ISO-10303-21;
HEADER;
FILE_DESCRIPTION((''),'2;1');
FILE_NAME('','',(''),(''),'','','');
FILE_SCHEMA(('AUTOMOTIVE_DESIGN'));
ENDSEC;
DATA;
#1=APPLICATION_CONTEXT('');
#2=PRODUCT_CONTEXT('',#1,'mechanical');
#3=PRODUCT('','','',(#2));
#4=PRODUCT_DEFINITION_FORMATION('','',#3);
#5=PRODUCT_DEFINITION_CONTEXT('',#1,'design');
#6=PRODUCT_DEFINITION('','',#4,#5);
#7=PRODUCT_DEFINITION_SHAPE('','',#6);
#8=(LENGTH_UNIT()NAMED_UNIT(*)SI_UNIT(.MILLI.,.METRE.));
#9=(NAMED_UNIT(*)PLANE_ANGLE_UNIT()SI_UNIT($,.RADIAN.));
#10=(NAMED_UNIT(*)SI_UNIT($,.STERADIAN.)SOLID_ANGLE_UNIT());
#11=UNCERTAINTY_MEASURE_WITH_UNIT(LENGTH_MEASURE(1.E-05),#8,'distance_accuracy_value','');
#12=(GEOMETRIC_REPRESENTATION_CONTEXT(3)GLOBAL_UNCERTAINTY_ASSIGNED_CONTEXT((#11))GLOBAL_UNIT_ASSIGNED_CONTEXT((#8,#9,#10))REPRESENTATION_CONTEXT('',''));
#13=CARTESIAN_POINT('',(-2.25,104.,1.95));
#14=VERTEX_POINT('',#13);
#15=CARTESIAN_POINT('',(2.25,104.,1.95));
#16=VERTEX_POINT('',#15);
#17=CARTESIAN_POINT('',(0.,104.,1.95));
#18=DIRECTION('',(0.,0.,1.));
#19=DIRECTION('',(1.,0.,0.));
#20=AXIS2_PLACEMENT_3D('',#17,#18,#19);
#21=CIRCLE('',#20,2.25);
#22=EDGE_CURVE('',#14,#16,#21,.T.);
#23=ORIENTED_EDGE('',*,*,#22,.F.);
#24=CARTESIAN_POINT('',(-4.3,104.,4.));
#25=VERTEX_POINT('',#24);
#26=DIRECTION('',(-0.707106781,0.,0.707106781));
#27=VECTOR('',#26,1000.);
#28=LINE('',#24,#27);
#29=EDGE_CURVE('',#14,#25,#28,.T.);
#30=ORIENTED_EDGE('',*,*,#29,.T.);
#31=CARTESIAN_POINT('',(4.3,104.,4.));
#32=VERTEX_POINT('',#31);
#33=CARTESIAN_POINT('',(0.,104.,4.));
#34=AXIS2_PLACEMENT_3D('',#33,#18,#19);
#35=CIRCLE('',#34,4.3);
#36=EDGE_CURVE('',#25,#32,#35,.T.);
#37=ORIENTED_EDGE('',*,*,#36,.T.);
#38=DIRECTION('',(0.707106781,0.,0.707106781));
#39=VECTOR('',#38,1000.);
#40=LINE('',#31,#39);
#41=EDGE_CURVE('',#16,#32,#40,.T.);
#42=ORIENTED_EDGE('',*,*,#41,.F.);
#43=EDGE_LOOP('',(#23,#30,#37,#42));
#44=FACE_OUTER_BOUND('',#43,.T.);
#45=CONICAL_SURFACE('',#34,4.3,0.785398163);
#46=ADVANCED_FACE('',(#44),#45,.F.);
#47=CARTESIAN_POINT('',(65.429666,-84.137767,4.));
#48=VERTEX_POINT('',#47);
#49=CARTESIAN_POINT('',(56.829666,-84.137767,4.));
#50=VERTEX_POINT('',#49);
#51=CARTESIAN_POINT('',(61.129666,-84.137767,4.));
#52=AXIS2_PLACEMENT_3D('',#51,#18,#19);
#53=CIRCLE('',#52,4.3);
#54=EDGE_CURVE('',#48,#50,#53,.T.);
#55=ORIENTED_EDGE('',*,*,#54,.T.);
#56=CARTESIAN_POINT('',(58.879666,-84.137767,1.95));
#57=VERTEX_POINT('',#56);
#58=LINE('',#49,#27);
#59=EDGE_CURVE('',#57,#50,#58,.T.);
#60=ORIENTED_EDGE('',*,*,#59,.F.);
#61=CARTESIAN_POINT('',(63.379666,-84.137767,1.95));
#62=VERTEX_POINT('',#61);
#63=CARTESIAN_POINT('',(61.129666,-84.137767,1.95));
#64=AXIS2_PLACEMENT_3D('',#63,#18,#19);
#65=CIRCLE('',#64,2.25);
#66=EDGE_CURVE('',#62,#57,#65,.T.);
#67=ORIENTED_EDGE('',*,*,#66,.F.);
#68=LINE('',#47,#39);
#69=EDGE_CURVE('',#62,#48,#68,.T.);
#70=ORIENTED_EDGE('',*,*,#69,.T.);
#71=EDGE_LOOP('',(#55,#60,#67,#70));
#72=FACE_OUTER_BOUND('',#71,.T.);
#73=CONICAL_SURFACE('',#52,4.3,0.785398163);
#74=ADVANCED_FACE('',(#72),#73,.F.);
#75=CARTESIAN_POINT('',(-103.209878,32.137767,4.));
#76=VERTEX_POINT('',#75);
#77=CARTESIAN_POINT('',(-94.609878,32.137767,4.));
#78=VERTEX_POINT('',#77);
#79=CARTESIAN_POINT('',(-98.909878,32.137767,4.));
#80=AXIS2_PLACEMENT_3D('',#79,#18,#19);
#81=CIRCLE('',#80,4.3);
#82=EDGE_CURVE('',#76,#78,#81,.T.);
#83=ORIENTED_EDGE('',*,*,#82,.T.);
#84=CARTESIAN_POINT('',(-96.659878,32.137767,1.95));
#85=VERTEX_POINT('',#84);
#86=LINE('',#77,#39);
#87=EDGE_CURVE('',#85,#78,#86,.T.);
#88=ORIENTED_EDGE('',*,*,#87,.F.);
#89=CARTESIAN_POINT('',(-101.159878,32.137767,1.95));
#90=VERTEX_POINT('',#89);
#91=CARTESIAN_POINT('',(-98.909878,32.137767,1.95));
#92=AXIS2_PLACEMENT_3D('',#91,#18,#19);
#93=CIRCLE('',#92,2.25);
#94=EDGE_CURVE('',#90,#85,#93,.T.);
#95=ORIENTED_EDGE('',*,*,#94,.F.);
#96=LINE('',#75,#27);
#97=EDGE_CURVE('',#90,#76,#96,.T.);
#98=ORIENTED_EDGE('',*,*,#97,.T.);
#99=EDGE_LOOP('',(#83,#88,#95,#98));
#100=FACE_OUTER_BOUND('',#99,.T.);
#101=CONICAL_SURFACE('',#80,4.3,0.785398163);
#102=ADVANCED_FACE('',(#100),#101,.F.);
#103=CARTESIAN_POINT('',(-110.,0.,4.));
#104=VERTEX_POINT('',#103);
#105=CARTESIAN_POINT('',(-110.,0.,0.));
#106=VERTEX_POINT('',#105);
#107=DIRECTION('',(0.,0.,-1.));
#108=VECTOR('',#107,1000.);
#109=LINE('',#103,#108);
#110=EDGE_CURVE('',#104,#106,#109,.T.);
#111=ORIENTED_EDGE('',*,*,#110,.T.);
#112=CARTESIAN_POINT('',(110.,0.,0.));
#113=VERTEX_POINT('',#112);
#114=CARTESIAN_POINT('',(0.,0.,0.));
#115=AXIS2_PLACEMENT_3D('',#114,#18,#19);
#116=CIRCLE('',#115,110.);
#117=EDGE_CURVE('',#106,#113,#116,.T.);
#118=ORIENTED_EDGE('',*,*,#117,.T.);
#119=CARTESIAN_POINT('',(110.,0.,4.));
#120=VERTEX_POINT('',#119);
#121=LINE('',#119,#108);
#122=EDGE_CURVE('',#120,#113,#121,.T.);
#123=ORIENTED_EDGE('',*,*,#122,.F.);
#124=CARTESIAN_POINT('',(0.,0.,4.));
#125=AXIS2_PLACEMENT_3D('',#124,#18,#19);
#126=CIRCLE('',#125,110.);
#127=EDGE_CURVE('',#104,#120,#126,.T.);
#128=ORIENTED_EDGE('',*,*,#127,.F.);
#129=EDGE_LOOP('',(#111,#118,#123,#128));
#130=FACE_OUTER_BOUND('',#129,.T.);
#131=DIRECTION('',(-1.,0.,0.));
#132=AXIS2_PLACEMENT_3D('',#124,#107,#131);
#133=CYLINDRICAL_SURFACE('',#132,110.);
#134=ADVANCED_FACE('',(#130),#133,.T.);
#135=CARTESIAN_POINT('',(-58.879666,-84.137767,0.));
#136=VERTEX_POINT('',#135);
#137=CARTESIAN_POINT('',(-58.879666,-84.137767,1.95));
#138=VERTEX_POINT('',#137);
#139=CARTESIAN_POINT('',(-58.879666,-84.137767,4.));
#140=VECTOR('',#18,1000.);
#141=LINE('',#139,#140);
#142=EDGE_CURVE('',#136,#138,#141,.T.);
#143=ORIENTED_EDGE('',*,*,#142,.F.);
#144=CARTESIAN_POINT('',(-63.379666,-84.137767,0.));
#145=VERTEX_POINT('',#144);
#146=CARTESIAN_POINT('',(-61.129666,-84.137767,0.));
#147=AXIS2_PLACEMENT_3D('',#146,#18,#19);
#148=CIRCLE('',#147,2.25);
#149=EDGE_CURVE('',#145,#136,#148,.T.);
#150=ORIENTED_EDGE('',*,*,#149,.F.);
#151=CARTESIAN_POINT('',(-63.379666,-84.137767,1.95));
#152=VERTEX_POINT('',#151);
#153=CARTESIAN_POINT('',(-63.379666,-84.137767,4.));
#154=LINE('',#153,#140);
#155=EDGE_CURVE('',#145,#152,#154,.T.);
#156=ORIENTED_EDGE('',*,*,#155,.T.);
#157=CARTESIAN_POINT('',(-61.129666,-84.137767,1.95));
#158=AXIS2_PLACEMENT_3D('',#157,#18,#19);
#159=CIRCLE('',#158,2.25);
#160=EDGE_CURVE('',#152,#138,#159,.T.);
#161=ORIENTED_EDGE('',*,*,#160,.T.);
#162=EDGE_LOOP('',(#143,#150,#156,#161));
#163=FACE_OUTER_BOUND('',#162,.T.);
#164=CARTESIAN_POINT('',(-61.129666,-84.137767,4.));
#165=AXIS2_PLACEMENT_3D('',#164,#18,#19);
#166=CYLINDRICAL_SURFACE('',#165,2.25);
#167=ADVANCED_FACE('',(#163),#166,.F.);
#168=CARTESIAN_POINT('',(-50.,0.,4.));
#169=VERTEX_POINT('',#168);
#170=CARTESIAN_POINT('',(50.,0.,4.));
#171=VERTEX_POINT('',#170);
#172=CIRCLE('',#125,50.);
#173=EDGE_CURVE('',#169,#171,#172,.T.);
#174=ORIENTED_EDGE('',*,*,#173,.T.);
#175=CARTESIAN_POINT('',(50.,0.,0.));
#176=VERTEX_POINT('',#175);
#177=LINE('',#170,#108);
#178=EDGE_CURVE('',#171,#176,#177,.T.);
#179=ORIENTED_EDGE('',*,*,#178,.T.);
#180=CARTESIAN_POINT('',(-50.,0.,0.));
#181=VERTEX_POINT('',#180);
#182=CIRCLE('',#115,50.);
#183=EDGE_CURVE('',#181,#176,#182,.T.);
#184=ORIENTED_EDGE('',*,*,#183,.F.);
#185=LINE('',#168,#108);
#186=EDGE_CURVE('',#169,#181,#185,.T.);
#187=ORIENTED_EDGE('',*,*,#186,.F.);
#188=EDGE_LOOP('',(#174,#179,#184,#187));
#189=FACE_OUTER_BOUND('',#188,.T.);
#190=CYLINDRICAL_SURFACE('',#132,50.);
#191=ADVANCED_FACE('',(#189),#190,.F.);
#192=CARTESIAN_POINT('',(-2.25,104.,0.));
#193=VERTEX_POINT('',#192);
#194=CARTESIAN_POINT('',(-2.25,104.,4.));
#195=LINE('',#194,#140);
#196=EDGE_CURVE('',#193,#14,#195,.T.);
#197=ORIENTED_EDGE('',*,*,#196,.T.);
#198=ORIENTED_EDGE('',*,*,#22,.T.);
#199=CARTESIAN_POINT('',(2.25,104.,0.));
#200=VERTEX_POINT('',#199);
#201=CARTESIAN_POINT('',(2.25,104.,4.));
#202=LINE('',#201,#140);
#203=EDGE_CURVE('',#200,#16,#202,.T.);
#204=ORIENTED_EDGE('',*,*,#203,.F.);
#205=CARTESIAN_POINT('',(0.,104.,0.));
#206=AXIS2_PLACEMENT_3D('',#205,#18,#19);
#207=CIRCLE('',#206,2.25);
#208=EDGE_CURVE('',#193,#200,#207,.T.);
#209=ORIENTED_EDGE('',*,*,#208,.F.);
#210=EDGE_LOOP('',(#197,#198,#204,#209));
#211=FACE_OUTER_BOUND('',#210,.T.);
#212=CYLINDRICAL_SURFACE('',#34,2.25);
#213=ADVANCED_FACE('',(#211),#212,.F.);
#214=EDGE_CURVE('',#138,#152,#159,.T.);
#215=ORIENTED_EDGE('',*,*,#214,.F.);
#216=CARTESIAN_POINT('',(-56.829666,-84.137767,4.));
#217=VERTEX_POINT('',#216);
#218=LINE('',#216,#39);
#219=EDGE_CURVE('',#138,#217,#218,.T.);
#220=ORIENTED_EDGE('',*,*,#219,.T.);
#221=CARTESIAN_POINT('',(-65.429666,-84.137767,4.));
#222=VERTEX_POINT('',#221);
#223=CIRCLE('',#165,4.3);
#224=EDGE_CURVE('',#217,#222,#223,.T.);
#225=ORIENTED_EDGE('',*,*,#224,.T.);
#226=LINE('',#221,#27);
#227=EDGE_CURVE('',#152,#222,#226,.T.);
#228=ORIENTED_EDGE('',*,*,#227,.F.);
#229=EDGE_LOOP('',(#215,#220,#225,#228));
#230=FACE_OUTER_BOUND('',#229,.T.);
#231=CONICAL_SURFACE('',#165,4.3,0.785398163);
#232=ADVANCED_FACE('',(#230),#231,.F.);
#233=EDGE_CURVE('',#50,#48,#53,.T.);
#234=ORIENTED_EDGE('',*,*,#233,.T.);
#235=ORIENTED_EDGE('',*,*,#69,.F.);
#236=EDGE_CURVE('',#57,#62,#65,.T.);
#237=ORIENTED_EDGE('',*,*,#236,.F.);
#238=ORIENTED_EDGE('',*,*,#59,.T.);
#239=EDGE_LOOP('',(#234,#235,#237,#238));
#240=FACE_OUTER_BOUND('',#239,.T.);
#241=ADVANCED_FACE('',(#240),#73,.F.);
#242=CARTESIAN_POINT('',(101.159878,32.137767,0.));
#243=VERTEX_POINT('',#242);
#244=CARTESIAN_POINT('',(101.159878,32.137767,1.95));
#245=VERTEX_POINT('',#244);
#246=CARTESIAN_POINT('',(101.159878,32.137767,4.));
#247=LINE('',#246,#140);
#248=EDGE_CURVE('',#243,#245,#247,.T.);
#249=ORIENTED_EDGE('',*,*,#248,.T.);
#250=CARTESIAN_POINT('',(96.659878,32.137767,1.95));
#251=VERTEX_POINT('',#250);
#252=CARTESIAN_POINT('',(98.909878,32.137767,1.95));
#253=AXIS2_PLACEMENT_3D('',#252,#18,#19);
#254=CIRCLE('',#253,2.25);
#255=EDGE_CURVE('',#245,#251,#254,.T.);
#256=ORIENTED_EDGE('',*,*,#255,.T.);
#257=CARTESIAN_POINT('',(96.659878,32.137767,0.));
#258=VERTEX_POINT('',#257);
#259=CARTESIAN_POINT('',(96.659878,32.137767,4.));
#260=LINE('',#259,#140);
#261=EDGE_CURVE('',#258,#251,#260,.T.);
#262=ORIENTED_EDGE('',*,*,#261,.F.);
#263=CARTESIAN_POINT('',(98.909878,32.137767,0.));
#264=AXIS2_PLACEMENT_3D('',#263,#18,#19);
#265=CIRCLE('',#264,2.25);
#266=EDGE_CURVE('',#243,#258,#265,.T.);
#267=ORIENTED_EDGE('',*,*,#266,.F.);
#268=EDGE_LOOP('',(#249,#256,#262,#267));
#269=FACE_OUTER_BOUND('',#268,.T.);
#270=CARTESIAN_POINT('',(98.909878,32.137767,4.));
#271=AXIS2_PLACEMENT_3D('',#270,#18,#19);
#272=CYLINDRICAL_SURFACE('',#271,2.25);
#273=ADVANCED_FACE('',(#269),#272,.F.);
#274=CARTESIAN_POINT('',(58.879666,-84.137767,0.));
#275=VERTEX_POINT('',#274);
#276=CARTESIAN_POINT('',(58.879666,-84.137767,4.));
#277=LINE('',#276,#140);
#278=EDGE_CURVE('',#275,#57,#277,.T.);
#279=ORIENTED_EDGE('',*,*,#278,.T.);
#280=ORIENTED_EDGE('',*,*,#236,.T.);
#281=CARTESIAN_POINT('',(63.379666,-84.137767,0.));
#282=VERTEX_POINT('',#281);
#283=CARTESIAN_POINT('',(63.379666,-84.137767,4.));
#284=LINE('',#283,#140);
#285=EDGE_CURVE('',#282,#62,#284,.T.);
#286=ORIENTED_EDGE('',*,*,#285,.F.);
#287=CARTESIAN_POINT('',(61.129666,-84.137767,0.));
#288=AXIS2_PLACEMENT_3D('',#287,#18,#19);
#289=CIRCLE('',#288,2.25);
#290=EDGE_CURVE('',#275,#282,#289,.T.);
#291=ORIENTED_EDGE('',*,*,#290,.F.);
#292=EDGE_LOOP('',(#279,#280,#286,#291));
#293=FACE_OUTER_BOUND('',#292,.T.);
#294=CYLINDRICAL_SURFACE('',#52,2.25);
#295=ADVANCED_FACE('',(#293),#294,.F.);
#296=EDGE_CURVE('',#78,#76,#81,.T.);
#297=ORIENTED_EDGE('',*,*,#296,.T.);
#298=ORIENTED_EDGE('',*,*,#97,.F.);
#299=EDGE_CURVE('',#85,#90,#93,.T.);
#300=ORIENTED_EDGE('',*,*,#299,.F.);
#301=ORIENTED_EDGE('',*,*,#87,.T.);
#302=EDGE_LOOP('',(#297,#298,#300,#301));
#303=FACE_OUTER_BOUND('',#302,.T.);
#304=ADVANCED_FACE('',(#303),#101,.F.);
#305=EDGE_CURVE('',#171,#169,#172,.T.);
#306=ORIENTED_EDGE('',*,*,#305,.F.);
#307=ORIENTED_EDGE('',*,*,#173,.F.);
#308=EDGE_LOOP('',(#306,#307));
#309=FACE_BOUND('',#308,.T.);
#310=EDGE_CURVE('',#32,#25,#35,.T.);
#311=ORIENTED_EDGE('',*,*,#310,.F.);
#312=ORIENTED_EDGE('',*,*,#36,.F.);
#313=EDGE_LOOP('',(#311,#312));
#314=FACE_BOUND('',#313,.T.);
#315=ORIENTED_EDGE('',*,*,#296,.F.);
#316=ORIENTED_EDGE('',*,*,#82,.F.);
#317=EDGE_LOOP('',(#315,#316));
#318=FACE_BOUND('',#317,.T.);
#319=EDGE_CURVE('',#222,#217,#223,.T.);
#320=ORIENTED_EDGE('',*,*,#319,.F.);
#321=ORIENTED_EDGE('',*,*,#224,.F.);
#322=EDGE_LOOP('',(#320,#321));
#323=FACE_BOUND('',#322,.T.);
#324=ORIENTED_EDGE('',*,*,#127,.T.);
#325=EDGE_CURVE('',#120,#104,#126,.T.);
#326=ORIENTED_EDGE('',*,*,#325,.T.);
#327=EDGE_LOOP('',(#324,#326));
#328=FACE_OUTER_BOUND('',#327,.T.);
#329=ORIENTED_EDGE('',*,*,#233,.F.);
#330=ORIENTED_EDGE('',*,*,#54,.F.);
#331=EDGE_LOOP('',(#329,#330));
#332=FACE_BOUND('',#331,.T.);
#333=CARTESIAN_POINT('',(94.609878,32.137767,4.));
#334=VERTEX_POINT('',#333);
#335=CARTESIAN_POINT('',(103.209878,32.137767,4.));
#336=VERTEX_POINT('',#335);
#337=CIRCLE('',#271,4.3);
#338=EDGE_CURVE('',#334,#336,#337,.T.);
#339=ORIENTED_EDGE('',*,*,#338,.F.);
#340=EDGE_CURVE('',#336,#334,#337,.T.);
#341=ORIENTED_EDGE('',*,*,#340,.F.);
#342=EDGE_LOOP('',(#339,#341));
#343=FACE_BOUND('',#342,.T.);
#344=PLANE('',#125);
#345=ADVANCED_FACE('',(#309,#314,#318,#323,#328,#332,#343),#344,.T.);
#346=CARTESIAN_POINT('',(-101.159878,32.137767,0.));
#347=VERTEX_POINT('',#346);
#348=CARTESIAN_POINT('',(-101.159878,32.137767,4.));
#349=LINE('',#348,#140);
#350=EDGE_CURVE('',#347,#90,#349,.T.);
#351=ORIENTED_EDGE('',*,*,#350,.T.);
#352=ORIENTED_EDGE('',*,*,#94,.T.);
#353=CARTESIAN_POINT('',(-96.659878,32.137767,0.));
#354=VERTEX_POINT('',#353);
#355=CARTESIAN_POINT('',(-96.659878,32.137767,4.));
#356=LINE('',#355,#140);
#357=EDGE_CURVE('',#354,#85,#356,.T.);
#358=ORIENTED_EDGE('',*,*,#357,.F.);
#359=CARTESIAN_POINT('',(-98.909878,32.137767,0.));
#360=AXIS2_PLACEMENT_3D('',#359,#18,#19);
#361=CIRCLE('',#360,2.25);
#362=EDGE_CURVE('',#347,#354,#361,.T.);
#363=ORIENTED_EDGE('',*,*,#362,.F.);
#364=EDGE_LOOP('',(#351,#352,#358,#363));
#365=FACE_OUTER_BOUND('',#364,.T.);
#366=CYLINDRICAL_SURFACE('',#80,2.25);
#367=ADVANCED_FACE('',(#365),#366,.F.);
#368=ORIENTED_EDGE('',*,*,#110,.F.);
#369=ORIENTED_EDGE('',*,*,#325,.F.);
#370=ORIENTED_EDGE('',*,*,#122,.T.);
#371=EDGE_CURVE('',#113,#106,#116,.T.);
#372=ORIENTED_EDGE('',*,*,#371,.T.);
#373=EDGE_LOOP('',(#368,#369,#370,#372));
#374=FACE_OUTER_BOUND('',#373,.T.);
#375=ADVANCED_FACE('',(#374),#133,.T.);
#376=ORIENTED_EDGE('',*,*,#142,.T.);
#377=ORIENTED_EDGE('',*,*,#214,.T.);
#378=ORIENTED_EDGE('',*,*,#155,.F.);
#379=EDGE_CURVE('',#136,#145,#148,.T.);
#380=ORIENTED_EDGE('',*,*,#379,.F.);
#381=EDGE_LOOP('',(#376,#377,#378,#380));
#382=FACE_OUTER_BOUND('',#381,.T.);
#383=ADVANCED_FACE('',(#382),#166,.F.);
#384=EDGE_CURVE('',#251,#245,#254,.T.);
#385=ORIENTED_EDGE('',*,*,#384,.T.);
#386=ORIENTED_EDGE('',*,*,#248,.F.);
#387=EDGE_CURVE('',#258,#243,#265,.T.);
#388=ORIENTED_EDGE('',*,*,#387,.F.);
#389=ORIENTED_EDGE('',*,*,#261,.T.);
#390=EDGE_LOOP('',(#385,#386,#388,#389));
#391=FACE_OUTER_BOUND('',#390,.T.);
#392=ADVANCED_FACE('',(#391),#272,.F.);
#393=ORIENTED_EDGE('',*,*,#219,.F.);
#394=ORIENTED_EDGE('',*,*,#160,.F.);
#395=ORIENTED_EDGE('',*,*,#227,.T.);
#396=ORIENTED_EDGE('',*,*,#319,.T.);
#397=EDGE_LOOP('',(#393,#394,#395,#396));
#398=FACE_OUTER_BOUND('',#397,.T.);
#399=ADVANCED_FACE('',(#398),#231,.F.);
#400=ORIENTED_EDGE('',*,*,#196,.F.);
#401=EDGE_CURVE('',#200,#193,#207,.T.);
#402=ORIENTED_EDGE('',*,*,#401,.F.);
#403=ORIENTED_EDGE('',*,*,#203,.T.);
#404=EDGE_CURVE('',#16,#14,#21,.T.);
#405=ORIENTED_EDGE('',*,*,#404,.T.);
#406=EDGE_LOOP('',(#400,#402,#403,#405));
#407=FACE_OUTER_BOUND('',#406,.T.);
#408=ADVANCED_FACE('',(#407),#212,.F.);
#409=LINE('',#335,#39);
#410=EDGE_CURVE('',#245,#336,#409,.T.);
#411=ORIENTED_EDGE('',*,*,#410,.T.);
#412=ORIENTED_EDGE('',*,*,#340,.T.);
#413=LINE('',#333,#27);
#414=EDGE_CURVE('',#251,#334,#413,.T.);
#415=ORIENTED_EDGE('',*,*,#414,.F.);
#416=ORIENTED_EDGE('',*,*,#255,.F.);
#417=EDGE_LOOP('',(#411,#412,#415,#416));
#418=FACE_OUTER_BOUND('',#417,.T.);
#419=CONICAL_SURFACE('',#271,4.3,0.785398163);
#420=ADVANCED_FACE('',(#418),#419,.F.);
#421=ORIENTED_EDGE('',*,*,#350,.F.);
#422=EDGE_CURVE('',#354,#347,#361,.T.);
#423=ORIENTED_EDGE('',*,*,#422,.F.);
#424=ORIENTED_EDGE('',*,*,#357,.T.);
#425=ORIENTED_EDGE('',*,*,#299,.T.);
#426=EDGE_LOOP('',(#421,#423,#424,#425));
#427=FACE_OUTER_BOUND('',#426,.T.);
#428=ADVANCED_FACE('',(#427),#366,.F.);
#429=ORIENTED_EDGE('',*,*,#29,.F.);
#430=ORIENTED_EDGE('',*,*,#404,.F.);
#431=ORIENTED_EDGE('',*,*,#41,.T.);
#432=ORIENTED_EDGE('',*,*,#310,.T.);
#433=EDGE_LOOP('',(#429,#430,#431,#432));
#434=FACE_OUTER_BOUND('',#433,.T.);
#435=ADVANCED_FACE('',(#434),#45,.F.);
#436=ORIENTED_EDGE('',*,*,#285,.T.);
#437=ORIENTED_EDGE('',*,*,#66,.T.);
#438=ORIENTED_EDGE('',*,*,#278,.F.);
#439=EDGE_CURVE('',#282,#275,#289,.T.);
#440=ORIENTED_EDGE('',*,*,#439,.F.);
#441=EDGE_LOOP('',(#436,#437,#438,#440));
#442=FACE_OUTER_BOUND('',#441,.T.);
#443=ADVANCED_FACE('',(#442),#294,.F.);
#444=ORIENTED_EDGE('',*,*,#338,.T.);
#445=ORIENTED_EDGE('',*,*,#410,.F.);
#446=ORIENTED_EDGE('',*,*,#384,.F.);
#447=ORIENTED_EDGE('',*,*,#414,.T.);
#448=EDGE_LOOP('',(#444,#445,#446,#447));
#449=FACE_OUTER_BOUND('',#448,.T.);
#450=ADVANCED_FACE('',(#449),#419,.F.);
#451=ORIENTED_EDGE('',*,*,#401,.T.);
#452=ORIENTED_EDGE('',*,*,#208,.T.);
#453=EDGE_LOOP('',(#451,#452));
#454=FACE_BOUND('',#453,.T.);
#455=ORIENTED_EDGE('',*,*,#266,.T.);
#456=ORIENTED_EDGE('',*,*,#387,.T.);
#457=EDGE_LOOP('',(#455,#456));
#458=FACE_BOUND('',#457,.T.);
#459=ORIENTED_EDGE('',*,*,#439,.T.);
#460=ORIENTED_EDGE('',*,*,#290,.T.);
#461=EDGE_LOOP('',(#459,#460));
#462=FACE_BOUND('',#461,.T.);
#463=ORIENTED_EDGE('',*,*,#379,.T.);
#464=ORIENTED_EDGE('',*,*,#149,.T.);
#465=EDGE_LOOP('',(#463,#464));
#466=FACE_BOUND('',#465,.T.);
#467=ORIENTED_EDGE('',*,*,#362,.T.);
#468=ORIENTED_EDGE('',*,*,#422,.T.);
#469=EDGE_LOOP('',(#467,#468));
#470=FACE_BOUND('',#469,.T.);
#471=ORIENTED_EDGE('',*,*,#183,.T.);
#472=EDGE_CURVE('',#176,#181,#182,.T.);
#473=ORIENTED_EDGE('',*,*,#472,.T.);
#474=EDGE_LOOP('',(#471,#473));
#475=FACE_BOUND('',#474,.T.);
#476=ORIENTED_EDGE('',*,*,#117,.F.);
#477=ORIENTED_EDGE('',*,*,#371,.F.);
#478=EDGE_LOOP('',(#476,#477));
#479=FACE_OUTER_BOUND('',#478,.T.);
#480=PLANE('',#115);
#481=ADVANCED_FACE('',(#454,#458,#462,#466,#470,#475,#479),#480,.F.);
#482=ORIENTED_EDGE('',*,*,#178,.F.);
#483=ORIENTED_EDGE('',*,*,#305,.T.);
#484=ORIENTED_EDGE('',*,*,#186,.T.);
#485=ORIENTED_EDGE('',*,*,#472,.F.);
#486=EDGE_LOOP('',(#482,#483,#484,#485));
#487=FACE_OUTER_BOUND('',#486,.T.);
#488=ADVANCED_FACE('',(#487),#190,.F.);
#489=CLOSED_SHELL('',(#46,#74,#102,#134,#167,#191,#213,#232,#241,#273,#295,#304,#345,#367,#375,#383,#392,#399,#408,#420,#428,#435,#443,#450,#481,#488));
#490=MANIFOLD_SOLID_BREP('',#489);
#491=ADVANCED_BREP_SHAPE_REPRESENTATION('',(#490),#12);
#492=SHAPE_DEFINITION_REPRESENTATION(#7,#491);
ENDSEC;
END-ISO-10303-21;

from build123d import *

# Parameters (mm, degrees)
SKETCH1_R                                 = 110
SKETCH1_R_2                               = 50
BOSS_EXTRUDE1_DEPTH                       = 4
HOLE_SIZE_PER_CROSS_SLOTTED_COUNT_2_COUNT = 2
HOLE_SIZE_PER_CROSS_SLOTTED_COUNT_2_PITCH = 122.259332477
HOLE_SIZE_PER_CROSS_SLOTTED_COUNT_3_COUNT = 2
HOLE_SIZE_PER_CROSS_SLOTTED_COUNT_3_PITCH = 197.819755389
HOLE_SIZE_PER_CROSS_SLOTTED_COUNT_4_COUNT = 2
HOLE_SIZE_PER_CROSS_SLOTTED_COUNT_4_PITCH = 197.819755389
HOLE_SIZE_PER_CROSS_SLOTTED_COUNT_5_COUNT = 2
HOLE_SIZE_PER_CROSS_SLOTTED_COUNT_5_PITCH = 122.259332477


with BuildPart() as part:
    # Sketch1 → Boss-Extrude1 (new body)
    with BuildSketch(Plane.XY):
        Circle(SKETCH1_R)
        Circle(SKETCH1_R_2, mode=Mode.SUBTRACT)
    extrude(amount=BOSS_EXTRUDE1_DEPTH)

    # Sketch5 → Hole Size (% per cross) Slotted Countersunk Wood Screw Type1 (revolve, cut)
    with BuildSketch(Plane(origin=(0, 104, 4), x_dir=(0, -1, 0), z_dir=(1, 0, 0))):
        Polygon((0, 0), (0, 4), (2.25, 4), (2.25, 2.05), (4.3, 0), align=None)
    hole_size_per_cross_slotted_countersu = revolve(axis=Axis((0, 104, 10.35), (0, 0, -1)), mode=Mode.SUBTRACT)

    # Hole Size _ per cross_ Slotted Count 2: Hole Size (% per cross) Slotted Countersunk Wood Screw Type1 ×2
    with Locations(*[Vector(0.8090169943749717, -0.5877852522924399, 0) * (i * HOLE_SIZE_PER_CROSS_SLOTTED_COUNT_2_PITCH) for i in range(1, HOLE_SIZE_PER_CROSS_SLOTTED_COUNT_2_COUNT)]):
        add(hole_size_per_cross_slotted_countersu, mode=Mode.SUBTRACT)

    # Hole Size _ per cross_ Slotted Count 3: Hole Size (% per cross) Slotted Countersunk Wood Screw Type1 ×2
    with Locations(*[Vector(0.3090169943749865, -0.9510565162951409, 0) * (i * HOLE_SIZE_PER_CROSS_SLOTTED_COUNT_3_PITCH) for i in range(1, HOLE_SIZE_PER_CROSS_SLOTTED_COUNT_3_COUNT)]):
        add(hole_size_per_cross_slotted_countersu, mode=Mode.SUBTRACT)

    # Hole Size _ per cross_ Slotted Count 4: Hole Size (% per cross) Slotted Countersunk Wood Screw Type1 ×2
    with Locations(*[Vector(-0.30901699437490837, -0.9510565162951663, 0) * (i * HOLE_SIZE_PER_CROSS_SLOTTED_COUNT_4_PITCH) for i in range(1, HOLE_SIZE_PER_CROSS_SLOTTED_COUNT_4_COUNT)]):
        add(hole_size_per_cross_slotted_countersu, mode=Mode.SUBTRACT)

    # Hole Size _ per cross_ Slotted Count 5: Hole Size (% per cross) Slotted Countersunk Wood Screw Type1 ×2
    with Locations(*[Vector(-0.8090169943749234, -0.5877852522925062, 0) * (i * HOLE_SIZE_PER_CROSS_SLOTTED_COUNT_5_PITCH) for i in range(1, HOLE_SIZE_PER_CROSS_SLOTTED_COUNT_5_COUNT)]):
        add(hole_size_per_cross_slotted_countersu, mode=Mode.SUBTRACT)


solid = part.part
